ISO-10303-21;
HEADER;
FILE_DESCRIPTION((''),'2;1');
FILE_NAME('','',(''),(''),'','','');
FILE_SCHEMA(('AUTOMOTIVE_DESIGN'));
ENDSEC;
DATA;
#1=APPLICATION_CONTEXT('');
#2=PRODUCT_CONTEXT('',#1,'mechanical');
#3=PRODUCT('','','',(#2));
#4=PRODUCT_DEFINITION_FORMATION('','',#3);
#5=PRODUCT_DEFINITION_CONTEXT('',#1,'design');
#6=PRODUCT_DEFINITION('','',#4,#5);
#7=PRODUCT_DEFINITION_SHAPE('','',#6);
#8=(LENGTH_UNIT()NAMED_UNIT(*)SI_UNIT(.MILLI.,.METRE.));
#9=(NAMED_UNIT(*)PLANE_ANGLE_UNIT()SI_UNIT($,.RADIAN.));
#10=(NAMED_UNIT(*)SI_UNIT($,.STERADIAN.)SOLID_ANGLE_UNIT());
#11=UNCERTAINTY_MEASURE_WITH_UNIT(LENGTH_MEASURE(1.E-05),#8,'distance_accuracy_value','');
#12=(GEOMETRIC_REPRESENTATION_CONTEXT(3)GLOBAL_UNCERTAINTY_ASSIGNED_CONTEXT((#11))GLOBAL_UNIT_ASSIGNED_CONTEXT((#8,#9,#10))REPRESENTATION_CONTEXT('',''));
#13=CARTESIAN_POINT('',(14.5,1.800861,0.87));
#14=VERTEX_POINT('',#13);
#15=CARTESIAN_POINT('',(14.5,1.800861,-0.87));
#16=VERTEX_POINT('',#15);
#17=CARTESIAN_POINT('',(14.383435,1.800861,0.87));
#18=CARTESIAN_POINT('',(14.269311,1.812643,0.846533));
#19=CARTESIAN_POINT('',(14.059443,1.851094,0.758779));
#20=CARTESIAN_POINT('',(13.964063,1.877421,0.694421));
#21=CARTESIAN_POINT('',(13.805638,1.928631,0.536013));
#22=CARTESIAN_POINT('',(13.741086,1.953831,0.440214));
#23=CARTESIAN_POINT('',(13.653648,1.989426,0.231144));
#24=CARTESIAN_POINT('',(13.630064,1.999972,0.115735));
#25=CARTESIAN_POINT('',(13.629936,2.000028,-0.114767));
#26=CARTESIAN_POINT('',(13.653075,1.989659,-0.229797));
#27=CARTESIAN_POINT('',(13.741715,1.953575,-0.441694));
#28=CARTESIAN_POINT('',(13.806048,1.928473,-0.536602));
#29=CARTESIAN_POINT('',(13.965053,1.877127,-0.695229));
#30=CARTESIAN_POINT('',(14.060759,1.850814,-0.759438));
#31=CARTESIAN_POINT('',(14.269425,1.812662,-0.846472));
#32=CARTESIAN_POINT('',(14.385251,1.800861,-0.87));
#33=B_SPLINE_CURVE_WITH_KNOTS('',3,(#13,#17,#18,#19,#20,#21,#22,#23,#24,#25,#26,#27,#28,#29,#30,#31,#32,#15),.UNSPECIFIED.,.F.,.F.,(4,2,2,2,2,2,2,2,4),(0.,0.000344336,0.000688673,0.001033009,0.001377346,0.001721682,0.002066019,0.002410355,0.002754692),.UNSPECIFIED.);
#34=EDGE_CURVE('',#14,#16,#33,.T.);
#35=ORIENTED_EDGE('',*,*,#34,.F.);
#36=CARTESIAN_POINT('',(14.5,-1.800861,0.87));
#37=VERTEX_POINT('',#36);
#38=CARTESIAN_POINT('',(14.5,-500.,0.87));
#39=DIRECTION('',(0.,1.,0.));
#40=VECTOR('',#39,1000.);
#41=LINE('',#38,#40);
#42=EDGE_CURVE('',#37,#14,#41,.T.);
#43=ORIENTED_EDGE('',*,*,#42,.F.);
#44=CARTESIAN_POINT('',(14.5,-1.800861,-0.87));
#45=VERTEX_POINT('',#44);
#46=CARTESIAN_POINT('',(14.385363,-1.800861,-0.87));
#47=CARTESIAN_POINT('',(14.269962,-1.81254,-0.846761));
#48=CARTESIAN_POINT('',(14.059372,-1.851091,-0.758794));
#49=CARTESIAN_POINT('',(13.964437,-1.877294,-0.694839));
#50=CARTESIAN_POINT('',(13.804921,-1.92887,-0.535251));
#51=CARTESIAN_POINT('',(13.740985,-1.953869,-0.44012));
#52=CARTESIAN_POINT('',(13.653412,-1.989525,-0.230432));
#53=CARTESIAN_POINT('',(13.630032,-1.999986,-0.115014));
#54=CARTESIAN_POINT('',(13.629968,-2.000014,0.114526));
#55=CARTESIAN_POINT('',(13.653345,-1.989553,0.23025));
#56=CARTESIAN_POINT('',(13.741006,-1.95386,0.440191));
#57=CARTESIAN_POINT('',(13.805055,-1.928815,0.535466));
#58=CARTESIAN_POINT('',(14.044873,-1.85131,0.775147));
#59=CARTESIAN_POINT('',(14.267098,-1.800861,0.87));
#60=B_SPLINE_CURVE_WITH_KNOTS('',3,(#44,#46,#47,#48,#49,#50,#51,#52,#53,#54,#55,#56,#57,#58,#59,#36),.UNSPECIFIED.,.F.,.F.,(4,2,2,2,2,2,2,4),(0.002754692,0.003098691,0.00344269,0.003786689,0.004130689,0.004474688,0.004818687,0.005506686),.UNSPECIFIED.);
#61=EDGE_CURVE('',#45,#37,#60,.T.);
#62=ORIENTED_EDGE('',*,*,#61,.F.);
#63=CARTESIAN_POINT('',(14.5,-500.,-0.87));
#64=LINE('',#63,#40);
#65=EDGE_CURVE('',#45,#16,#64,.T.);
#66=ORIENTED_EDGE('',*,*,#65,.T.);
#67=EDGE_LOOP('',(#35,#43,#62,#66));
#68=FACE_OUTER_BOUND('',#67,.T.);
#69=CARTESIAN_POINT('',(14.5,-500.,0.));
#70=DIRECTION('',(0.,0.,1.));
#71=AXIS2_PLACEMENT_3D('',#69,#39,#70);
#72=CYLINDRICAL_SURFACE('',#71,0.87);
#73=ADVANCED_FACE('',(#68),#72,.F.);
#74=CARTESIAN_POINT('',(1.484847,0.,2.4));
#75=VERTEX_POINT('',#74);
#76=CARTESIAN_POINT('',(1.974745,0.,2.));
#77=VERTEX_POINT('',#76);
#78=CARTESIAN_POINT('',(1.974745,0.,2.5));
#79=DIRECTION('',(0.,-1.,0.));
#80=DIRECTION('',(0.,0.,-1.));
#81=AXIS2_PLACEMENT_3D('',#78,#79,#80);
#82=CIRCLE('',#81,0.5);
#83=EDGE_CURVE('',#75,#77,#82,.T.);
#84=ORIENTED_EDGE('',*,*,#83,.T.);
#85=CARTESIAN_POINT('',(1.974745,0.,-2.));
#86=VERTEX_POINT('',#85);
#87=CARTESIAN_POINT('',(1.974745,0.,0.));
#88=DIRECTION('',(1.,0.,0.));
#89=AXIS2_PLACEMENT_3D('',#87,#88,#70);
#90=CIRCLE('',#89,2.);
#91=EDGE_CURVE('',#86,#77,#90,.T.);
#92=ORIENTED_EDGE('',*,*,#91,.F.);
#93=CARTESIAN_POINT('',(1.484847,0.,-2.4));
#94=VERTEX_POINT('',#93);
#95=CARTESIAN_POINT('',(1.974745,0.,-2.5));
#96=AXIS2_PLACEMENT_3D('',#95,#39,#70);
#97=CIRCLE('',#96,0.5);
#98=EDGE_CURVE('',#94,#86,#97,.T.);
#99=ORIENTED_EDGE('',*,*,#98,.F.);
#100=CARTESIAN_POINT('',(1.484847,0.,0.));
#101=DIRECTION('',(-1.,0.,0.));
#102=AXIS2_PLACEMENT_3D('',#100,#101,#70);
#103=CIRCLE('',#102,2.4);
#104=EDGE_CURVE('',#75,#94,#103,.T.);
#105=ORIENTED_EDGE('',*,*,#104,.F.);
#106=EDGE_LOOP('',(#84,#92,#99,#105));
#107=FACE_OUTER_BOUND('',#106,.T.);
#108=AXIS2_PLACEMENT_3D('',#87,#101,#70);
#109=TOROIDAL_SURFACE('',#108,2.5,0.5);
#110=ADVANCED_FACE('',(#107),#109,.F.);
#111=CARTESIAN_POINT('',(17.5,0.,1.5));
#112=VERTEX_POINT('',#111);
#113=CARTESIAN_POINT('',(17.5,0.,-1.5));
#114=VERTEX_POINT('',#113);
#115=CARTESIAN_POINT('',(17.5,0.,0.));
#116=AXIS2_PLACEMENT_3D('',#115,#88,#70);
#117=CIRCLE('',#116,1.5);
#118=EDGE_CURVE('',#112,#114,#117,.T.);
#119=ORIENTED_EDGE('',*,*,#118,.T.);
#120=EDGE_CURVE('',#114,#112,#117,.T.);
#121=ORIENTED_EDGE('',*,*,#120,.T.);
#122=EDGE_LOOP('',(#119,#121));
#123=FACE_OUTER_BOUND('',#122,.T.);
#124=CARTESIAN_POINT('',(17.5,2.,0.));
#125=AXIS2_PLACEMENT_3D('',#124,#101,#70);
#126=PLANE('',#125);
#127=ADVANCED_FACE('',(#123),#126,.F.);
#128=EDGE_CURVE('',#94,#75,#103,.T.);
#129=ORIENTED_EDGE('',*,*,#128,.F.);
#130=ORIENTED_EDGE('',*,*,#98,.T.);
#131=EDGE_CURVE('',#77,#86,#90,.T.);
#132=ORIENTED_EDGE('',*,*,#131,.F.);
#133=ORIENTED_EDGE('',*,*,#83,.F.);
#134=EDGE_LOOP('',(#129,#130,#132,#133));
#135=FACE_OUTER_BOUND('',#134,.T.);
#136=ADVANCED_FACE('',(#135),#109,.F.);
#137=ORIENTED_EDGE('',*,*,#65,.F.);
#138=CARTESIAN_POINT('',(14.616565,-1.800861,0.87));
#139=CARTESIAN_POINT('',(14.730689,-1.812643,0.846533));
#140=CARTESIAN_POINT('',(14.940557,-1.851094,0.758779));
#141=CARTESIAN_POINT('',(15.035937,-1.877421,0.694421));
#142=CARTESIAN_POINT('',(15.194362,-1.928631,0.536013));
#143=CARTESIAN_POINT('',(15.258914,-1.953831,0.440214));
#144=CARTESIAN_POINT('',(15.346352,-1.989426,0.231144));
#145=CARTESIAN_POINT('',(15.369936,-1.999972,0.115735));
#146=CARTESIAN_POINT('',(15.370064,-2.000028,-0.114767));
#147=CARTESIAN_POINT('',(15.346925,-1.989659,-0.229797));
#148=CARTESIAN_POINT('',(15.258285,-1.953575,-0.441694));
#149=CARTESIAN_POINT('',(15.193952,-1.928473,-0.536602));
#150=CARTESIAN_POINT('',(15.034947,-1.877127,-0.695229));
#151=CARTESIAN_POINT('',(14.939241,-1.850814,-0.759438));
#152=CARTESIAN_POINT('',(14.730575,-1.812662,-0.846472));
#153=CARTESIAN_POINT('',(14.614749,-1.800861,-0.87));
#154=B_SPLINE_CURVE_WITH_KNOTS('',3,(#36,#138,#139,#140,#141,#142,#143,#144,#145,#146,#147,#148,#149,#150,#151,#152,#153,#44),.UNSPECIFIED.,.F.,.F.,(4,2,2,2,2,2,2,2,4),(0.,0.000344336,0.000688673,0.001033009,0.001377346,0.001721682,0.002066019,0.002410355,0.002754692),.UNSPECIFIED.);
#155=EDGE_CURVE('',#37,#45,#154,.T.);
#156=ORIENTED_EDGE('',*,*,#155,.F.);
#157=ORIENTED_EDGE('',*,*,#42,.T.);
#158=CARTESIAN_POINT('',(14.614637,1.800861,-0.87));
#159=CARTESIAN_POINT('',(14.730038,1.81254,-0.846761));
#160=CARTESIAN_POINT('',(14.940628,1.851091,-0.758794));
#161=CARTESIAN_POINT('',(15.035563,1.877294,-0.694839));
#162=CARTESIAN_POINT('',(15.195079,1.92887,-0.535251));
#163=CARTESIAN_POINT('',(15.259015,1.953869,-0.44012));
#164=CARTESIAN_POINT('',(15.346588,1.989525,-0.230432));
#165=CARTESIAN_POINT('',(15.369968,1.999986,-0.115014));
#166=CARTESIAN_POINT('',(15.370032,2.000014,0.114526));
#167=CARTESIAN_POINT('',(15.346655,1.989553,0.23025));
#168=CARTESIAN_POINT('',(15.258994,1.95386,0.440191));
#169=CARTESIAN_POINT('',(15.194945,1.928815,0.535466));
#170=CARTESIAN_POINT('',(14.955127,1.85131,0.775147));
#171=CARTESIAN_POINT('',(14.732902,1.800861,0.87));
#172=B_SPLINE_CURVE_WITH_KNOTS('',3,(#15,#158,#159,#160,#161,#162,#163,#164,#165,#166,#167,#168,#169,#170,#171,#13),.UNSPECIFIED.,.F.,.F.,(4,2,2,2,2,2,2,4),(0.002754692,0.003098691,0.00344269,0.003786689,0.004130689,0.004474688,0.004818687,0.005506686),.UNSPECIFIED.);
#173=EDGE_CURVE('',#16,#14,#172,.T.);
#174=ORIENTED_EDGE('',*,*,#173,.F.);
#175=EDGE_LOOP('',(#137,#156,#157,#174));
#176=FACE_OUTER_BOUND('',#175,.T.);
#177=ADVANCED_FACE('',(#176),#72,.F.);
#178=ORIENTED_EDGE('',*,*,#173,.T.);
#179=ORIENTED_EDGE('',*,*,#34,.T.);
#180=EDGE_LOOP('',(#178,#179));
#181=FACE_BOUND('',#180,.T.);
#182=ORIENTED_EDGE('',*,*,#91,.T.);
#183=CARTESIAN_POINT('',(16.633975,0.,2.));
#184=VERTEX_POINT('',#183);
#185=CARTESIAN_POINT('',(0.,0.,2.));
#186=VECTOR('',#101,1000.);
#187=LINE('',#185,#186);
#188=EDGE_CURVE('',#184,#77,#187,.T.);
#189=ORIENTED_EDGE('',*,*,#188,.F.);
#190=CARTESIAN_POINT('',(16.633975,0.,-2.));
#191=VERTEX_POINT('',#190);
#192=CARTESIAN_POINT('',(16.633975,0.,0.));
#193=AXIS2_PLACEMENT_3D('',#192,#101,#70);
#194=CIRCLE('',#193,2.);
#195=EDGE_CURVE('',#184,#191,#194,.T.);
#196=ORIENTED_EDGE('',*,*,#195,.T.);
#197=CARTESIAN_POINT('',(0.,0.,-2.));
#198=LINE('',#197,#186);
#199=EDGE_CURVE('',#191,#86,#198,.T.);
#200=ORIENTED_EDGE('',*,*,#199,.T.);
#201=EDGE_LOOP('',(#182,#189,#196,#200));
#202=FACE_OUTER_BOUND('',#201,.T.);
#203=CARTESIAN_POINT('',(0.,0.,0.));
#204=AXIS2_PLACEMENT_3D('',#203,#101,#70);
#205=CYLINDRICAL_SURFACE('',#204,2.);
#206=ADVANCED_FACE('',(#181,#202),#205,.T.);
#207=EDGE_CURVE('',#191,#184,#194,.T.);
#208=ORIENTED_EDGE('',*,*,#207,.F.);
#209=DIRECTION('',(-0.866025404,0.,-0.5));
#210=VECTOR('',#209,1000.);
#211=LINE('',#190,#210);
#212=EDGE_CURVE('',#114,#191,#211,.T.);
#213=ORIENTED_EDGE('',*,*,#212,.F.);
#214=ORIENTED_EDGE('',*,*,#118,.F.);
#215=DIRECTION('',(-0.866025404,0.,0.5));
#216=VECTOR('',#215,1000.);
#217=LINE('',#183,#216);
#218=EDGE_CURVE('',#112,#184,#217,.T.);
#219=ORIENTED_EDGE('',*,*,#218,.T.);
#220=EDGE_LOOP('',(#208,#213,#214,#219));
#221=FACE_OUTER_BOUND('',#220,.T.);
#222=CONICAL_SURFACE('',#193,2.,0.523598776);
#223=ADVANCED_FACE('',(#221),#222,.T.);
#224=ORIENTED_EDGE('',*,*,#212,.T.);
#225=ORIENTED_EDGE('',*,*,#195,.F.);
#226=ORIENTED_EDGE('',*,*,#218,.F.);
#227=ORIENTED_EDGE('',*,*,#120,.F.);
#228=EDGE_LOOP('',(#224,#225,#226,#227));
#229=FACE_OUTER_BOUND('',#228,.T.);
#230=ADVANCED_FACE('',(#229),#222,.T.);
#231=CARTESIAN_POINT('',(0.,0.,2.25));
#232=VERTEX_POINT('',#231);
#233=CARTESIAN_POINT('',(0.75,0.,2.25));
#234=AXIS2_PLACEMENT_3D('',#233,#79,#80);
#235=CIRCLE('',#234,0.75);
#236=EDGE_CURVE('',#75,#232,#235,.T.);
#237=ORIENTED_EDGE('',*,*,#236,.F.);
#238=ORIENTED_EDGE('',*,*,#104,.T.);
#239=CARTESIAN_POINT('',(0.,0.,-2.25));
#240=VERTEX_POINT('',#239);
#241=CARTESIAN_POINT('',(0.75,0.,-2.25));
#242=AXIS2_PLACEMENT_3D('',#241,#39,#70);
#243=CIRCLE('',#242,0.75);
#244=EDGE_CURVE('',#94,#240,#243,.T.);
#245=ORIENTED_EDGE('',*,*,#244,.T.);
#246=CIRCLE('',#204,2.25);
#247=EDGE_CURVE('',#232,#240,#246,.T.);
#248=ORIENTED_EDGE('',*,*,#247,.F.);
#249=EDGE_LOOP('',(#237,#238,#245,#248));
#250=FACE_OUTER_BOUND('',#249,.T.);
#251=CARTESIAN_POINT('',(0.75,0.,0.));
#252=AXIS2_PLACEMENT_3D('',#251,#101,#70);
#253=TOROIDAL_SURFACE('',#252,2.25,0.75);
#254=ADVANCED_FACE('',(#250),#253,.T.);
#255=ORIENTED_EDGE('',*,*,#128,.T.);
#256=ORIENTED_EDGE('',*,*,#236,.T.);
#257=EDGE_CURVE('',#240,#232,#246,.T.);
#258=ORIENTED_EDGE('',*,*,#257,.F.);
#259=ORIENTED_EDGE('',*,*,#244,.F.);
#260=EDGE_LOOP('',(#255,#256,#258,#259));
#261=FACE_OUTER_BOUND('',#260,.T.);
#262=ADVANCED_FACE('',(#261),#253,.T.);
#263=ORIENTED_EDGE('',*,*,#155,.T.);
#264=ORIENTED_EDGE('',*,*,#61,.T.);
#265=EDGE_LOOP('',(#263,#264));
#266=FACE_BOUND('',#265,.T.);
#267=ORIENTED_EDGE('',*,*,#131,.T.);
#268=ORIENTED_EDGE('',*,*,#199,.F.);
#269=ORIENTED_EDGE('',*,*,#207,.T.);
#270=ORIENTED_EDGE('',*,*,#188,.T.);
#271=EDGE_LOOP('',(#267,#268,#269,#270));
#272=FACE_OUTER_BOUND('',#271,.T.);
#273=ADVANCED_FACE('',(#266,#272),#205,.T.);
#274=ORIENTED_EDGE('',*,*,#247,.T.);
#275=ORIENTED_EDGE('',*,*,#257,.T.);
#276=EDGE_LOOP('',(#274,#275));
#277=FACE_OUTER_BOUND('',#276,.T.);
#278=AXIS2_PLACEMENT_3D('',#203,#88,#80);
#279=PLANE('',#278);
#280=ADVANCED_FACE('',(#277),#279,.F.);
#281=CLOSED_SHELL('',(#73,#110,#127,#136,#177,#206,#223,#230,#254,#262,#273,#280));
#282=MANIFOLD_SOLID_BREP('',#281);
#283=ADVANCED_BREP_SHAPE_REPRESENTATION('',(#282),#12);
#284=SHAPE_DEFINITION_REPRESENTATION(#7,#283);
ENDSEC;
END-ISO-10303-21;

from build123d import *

# Parameters (mm, degrees)
FILLET_1_R          = 0.5
CHAMFER_1_SIZE      = 0.866025404
CHAMFER_1_SIZE2     = 0.5
SKETCH_2_R          = 0.87
CUT_EXTRUDE_1_DEPTH = 500


with BuildPart() as part:
    # 草图1 → Revolve 700 (revolve)
    with BuildSketch(Plane.XY, mode=Mode.PRIVATE) as revolve_700_sk:
        with BuildLine():
            Line((0, 0), (17.5, 0))
            Line((17.5, 0), (17.5, 2))
            Line((17.5, 2), (1.5, 2))
            Line((1.5, 2), (1.5, 2.25))
            ThreePointArc((1.5, 2.25), (0.75, 3), (0, 2.25))
            Line((0, 2.25), (0, 0))
        make_face()
    revolve(revolve_700_sk.sketch.rotate(Axis((0, 0, 0), (1, 0, 0)), 90), axis=Axis((0, 0, 0), (1, 0, 0)))

    # 圆角1
    fillet_1_edges = [part.edges().sort_by_distance(p)[0] for p in [
        (1.5, 0, -2),
    ]]
    fillet(fillet_1_edges, radius=FILLET_1_R)

    # 倒角1
    chamfer_1_edges = [part.edges().sort_by_distance(p)[0] for p in [
        (17.5, 0, -2),
    ]]
    chamfer_1_side = [part.faces().sort_by_distance(p)[0] for p in [
        (9.737372436, 0, -2),
    ]]
    chamfer(chamfer_1_edges, length=CHAMFER_1_SIZE, length2=CHAMFER_1_SIZE2, reference=chamfer_1_side[0])

    # 草图2 → 切除-拉伸1 (cut, symmetric)
    with BuildSketch(Plane(origin=(0, 0, 0), x_dir=(1, 0, 0), z_dir=(0, 1, 0))):
        with Locations(Location((14.5, 0, 0), (0, 0, 270))):
            Circle(SKETCH_2_R)
    extrude(amount=CUT_EXTRUDE_1_DEPTH, both=True, mode=Mode.SUBTRACT)


solid = part.part
